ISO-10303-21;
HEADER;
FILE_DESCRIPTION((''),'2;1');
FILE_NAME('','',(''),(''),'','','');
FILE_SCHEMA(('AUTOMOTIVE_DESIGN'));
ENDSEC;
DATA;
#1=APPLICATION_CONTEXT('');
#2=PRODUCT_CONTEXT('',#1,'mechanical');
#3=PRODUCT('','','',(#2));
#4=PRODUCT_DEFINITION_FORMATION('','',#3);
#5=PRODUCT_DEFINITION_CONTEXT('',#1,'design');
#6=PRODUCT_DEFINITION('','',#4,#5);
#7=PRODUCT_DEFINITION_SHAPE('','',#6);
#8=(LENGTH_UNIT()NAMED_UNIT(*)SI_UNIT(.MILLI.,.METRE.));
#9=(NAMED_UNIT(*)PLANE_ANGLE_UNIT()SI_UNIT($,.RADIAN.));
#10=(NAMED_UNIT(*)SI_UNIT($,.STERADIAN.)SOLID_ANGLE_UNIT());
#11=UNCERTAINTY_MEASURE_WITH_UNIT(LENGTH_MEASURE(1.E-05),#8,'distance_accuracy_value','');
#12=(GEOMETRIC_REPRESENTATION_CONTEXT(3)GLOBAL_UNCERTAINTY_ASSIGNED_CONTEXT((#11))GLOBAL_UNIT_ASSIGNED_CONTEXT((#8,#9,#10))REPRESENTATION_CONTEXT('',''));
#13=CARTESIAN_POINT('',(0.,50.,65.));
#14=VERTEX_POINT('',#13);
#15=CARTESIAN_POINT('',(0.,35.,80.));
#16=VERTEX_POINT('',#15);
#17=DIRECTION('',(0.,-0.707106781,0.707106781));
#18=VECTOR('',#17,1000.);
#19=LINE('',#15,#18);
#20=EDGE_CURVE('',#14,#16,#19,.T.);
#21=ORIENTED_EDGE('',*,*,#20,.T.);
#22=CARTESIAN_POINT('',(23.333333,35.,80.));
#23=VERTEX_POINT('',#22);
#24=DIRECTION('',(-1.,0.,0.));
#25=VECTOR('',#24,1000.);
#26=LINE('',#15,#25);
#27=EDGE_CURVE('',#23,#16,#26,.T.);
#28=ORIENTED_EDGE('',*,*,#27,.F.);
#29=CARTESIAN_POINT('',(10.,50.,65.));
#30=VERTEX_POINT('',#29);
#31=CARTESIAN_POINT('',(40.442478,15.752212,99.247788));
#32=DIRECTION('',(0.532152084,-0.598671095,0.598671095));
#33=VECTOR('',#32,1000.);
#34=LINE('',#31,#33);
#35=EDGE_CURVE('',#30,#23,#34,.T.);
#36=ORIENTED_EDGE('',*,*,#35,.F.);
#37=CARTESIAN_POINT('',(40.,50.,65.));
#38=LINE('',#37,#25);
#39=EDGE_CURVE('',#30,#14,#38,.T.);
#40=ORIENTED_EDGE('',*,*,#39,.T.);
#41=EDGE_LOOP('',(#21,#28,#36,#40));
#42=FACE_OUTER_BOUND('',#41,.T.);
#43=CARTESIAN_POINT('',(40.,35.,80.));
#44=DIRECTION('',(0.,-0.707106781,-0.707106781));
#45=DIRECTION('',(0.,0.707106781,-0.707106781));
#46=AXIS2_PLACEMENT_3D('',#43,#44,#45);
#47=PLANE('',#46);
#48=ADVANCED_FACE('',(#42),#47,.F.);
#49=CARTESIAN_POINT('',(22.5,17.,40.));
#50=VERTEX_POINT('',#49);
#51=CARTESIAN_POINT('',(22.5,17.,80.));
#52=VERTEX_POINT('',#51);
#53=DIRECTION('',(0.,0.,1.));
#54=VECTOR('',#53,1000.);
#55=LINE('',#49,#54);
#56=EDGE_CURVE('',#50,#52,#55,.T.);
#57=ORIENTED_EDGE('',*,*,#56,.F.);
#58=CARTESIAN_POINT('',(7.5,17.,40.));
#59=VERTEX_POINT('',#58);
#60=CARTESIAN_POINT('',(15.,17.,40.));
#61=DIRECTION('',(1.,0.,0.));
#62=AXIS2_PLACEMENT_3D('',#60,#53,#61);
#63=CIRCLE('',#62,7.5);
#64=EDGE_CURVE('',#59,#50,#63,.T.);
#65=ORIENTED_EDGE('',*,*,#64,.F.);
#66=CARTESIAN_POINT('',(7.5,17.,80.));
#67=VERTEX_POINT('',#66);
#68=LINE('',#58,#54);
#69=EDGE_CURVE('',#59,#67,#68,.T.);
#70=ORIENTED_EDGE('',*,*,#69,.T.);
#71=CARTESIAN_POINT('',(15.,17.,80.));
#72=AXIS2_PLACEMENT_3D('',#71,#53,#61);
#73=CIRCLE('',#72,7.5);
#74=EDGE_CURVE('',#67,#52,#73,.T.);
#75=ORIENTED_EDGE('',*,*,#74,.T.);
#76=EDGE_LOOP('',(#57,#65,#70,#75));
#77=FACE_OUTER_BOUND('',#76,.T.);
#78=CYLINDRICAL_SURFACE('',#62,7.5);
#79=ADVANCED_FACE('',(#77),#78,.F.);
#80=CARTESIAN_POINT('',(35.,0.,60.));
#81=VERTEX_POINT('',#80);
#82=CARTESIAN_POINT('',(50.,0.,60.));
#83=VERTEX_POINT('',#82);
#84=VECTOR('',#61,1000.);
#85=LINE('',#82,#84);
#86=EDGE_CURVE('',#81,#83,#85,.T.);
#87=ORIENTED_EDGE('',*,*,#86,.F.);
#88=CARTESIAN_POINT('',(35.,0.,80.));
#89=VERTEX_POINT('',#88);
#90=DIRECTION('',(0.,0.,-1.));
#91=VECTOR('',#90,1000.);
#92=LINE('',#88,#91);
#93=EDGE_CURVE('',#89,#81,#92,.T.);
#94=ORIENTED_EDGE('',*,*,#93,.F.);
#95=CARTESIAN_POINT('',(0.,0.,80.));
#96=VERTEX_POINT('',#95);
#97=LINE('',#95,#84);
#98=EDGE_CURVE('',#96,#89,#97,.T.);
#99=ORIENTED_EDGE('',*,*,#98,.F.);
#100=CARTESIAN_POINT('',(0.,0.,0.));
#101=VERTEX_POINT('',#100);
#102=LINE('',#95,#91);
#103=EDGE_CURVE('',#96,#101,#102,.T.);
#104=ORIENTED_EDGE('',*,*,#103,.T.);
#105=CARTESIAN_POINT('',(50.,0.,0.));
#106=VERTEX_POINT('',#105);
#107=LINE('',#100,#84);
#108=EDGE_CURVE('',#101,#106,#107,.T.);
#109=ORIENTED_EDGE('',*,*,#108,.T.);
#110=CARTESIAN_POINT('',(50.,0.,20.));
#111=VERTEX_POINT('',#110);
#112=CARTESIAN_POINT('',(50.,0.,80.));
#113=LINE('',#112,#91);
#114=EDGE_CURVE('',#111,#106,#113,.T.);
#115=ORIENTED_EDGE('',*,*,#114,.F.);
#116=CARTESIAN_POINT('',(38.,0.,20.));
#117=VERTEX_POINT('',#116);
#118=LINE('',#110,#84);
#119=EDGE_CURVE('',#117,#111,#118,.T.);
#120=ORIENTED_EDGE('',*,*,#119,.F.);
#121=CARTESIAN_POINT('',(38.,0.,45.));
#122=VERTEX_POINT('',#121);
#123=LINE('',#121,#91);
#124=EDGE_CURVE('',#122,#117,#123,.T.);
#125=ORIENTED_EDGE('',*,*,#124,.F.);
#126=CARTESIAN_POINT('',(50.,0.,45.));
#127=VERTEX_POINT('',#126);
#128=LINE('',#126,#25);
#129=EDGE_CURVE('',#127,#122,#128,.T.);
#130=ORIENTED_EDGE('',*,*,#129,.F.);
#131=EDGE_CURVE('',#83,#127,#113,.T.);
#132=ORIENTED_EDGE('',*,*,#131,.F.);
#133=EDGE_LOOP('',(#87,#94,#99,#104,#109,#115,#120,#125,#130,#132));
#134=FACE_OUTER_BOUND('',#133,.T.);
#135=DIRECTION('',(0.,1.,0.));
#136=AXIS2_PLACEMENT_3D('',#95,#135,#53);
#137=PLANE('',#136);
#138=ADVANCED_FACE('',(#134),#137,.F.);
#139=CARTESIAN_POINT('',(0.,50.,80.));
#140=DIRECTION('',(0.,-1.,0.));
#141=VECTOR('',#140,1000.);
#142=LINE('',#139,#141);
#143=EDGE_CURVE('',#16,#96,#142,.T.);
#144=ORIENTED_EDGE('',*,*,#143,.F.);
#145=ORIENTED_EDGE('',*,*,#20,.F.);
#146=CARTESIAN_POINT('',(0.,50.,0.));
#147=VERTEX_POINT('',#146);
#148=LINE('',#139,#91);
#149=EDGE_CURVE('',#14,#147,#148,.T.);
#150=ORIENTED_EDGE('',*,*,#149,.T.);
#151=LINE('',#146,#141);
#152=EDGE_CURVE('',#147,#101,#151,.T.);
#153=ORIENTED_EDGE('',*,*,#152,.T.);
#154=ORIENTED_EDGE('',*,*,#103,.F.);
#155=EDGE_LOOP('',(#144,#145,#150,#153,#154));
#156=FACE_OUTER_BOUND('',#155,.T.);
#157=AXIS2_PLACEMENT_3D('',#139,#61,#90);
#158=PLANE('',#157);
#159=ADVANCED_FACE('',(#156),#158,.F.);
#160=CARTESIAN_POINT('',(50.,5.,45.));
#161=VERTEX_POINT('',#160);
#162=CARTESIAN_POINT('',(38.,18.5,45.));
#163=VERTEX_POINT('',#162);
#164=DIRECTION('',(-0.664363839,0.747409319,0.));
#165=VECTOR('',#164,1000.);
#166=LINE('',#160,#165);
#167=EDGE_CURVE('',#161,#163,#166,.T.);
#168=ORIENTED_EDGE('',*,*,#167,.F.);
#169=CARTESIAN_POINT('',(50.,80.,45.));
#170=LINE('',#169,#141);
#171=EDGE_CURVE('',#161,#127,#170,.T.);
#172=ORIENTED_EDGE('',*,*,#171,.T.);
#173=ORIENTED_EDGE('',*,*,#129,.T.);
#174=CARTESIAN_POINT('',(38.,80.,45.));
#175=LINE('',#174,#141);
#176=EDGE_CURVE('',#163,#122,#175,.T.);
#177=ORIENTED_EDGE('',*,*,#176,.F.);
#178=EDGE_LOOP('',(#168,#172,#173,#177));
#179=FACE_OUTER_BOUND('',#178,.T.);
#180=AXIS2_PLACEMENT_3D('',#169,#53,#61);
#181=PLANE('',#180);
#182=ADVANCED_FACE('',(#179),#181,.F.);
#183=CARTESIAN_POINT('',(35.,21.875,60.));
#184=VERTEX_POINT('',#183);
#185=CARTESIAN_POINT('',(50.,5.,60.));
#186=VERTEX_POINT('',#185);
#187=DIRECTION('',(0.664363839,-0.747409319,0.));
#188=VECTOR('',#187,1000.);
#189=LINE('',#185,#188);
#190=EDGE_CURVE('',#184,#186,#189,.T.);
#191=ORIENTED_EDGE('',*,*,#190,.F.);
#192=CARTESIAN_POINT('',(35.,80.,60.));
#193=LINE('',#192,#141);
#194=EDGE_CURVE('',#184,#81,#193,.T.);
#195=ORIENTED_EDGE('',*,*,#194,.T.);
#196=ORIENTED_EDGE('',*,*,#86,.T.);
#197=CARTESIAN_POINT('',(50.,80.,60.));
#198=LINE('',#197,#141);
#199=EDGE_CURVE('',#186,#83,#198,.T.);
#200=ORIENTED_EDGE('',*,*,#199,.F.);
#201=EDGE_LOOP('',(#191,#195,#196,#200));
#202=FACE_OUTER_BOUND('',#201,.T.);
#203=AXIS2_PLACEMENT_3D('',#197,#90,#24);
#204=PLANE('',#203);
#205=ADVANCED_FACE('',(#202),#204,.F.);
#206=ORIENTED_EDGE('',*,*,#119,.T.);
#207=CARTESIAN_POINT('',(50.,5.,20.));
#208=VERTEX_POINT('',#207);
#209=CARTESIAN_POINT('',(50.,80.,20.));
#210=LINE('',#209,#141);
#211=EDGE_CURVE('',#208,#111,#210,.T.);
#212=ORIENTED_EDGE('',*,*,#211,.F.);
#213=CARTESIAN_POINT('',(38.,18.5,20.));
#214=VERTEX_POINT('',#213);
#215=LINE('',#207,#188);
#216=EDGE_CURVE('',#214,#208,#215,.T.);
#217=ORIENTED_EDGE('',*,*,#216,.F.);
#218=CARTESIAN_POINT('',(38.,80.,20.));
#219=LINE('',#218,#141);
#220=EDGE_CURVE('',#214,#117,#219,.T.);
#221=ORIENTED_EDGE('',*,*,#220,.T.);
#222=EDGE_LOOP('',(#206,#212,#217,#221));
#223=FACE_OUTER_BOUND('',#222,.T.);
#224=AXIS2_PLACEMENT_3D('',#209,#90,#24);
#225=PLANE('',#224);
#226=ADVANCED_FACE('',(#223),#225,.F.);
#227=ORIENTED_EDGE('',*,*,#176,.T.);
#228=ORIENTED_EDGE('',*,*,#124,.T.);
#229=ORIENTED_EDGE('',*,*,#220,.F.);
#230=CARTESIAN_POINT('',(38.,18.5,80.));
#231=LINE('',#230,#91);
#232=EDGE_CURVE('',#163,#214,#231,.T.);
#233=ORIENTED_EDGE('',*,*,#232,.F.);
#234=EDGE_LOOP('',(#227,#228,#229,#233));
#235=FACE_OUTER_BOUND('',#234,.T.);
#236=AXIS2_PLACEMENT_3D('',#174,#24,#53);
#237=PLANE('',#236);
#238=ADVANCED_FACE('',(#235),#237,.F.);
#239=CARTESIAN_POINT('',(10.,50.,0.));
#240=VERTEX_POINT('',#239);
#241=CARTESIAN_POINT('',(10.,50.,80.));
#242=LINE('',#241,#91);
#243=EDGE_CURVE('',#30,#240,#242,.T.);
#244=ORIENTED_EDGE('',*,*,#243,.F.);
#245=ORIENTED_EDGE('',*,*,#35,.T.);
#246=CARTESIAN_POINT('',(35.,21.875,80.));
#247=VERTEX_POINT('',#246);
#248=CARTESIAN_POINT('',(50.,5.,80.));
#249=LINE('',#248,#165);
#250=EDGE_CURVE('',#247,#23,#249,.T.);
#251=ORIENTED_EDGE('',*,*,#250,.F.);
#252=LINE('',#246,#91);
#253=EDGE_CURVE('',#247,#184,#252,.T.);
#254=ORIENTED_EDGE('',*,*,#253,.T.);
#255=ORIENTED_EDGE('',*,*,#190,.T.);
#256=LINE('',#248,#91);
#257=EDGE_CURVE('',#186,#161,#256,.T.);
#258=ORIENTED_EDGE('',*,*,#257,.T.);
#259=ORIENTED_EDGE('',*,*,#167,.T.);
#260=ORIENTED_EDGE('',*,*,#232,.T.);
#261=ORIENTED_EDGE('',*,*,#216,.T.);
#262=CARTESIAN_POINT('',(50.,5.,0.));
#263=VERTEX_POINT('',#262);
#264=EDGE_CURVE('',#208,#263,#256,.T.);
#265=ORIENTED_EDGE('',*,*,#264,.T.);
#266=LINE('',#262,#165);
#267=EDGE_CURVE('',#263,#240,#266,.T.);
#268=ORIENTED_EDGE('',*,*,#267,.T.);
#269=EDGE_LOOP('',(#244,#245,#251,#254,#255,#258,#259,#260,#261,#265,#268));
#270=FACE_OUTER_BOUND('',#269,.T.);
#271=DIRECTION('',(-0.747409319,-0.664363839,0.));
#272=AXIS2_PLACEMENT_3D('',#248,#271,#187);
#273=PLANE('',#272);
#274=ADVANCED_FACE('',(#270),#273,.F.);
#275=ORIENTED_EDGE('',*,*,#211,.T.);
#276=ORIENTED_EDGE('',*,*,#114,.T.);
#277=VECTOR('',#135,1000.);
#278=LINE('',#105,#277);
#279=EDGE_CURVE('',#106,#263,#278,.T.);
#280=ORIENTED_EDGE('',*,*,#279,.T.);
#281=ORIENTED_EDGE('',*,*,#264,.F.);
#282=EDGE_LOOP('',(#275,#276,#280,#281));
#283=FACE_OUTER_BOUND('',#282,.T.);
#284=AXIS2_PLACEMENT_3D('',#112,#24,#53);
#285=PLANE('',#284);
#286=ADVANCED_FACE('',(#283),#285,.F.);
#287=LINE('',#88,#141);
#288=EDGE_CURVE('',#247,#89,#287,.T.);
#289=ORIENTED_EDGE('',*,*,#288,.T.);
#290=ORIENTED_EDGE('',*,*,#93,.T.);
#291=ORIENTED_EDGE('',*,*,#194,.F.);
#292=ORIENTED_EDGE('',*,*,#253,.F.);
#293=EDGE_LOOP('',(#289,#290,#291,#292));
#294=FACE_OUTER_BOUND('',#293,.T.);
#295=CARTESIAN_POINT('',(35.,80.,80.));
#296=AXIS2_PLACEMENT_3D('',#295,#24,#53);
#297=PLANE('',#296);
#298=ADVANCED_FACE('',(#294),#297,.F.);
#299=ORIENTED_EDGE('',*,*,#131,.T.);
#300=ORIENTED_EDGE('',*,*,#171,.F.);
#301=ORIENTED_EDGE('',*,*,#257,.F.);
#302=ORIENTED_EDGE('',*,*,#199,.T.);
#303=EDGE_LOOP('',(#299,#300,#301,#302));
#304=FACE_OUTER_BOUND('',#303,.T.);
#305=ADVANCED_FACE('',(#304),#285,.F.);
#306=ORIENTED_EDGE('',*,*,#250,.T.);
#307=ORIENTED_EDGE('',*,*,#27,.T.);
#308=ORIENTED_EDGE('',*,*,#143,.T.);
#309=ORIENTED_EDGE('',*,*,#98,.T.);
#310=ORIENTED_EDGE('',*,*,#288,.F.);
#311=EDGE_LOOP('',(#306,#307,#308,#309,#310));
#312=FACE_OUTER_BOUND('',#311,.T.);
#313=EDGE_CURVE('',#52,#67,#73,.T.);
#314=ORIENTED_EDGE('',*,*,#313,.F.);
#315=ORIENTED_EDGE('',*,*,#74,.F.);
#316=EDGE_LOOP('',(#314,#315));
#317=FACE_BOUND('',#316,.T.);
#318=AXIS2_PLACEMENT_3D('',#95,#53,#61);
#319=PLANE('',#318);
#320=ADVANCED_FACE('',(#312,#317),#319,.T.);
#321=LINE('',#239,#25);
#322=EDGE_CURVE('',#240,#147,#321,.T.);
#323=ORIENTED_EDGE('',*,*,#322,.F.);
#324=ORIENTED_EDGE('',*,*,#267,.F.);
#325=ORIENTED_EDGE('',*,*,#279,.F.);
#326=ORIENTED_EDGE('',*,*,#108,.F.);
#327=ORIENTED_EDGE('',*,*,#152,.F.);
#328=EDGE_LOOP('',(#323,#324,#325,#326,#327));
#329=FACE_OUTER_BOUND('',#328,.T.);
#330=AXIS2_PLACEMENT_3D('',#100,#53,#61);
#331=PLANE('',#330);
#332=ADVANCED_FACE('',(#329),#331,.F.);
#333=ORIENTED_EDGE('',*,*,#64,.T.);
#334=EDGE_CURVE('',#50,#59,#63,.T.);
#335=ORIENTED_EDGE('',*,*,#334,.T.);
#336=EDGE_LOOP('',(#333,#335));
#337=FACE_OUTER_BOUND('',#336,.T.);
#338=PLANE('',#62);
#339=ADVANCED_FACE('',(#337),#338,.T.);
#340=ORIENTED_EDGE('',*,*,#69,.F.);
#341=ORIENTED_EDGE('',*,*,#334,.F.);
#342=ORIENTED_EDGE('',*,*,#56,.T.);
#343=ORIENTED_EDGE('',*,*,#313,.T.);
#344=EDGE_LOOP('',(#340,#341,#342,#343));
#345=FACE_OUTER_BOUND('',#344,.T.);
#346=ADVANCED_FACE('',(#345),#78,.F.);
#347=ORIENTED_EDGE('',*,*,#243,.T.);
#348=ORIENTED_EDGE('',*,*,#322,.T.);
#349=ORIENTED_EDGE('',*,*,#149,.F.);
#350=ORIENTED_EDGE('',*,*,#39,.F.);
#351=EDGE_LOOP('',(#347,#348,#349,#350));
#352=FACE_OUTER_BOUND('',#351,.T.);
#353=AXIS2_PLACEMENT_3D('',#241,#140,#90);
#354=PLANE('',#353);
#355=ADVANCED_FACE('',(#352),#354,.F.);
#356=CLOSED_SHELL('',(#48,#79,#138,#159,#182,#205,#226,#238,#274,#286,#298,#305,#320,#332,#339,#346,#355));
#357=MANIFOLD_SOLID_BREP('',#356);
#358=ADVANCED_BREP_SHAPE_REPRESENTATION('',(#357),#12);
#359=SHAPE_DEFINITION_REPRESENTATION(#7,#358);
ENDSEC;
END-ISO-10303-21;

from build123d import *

# Parameters (mm, degrees)
BRACKET_BODY_DEPTH          = 80
BASE_NOTCH_SKETCH_W         = 15
BASE_NOTCH_SKETCH_H         = 20
BASE_NOTCH_SKETCH_W_2       = 12
BASE_NOTCH_SKETCH_H_2       = 25
BASE_NOTCH_CUT_DEPTH        = 80
SIDE_HOLE_SKETCH_R          = 7.5
SIDE_HOLE_DEPTH             = 40
HALF_LENGTH_BEVEL_CUT_DEPTH = 40


with BuildPart() as part:
    # Bracket Profile Sketch → Bracket Body (new body)
    with BuildSketch(Plane.XY):
        Polygon((0, 0), (50, 0), (50, 5), (10, 50), (0, 50), align=None)
    extrude(amount=BRACKET_BODY_DEPTH)

    # Base Notch Sketch → Base Notch Cut (cut)
    with BuildSketch(Plane.XZ):
        with Locations((42.5, 70)):
            Rectangle(BASE_NOTCH_SKETCH_W, BASE_NOTCH_SKETCH_H)
        with Locations((44, 32.5)):
            Rectangle(BASE_NOTCH_SKETCH_W_2, BASE_NOTCH_SKETCH_H_2)
    extrude(amount=-BASE_NOTCH_CUT_DEPTH, mode=Mode.SUBTRACT)

    # Side Hole Sketch → Side Hole (cut)
    with BuildSketch(Plane.XY.offset(80)):
        with Locations((15, 17)):
            Circle(SIDE_HOLE_SKETCH_R)
    extrude(amount=-SIDE_HOLE_DEPTH, mode=Mode.SUBTRACT)

    # Half-Length Bevel Sketch → Half-Length Bevel Cut (cut)
    with BuildSketch(Plane.ZY):
        Polygon((80, 35), (65, 50), (80, 50), align=None)
    extrude(amount=-HALF_LENGTH_BEVEL_CUT_DEPTH, mode=Mode.SUBTRACT)


solid = part.part
